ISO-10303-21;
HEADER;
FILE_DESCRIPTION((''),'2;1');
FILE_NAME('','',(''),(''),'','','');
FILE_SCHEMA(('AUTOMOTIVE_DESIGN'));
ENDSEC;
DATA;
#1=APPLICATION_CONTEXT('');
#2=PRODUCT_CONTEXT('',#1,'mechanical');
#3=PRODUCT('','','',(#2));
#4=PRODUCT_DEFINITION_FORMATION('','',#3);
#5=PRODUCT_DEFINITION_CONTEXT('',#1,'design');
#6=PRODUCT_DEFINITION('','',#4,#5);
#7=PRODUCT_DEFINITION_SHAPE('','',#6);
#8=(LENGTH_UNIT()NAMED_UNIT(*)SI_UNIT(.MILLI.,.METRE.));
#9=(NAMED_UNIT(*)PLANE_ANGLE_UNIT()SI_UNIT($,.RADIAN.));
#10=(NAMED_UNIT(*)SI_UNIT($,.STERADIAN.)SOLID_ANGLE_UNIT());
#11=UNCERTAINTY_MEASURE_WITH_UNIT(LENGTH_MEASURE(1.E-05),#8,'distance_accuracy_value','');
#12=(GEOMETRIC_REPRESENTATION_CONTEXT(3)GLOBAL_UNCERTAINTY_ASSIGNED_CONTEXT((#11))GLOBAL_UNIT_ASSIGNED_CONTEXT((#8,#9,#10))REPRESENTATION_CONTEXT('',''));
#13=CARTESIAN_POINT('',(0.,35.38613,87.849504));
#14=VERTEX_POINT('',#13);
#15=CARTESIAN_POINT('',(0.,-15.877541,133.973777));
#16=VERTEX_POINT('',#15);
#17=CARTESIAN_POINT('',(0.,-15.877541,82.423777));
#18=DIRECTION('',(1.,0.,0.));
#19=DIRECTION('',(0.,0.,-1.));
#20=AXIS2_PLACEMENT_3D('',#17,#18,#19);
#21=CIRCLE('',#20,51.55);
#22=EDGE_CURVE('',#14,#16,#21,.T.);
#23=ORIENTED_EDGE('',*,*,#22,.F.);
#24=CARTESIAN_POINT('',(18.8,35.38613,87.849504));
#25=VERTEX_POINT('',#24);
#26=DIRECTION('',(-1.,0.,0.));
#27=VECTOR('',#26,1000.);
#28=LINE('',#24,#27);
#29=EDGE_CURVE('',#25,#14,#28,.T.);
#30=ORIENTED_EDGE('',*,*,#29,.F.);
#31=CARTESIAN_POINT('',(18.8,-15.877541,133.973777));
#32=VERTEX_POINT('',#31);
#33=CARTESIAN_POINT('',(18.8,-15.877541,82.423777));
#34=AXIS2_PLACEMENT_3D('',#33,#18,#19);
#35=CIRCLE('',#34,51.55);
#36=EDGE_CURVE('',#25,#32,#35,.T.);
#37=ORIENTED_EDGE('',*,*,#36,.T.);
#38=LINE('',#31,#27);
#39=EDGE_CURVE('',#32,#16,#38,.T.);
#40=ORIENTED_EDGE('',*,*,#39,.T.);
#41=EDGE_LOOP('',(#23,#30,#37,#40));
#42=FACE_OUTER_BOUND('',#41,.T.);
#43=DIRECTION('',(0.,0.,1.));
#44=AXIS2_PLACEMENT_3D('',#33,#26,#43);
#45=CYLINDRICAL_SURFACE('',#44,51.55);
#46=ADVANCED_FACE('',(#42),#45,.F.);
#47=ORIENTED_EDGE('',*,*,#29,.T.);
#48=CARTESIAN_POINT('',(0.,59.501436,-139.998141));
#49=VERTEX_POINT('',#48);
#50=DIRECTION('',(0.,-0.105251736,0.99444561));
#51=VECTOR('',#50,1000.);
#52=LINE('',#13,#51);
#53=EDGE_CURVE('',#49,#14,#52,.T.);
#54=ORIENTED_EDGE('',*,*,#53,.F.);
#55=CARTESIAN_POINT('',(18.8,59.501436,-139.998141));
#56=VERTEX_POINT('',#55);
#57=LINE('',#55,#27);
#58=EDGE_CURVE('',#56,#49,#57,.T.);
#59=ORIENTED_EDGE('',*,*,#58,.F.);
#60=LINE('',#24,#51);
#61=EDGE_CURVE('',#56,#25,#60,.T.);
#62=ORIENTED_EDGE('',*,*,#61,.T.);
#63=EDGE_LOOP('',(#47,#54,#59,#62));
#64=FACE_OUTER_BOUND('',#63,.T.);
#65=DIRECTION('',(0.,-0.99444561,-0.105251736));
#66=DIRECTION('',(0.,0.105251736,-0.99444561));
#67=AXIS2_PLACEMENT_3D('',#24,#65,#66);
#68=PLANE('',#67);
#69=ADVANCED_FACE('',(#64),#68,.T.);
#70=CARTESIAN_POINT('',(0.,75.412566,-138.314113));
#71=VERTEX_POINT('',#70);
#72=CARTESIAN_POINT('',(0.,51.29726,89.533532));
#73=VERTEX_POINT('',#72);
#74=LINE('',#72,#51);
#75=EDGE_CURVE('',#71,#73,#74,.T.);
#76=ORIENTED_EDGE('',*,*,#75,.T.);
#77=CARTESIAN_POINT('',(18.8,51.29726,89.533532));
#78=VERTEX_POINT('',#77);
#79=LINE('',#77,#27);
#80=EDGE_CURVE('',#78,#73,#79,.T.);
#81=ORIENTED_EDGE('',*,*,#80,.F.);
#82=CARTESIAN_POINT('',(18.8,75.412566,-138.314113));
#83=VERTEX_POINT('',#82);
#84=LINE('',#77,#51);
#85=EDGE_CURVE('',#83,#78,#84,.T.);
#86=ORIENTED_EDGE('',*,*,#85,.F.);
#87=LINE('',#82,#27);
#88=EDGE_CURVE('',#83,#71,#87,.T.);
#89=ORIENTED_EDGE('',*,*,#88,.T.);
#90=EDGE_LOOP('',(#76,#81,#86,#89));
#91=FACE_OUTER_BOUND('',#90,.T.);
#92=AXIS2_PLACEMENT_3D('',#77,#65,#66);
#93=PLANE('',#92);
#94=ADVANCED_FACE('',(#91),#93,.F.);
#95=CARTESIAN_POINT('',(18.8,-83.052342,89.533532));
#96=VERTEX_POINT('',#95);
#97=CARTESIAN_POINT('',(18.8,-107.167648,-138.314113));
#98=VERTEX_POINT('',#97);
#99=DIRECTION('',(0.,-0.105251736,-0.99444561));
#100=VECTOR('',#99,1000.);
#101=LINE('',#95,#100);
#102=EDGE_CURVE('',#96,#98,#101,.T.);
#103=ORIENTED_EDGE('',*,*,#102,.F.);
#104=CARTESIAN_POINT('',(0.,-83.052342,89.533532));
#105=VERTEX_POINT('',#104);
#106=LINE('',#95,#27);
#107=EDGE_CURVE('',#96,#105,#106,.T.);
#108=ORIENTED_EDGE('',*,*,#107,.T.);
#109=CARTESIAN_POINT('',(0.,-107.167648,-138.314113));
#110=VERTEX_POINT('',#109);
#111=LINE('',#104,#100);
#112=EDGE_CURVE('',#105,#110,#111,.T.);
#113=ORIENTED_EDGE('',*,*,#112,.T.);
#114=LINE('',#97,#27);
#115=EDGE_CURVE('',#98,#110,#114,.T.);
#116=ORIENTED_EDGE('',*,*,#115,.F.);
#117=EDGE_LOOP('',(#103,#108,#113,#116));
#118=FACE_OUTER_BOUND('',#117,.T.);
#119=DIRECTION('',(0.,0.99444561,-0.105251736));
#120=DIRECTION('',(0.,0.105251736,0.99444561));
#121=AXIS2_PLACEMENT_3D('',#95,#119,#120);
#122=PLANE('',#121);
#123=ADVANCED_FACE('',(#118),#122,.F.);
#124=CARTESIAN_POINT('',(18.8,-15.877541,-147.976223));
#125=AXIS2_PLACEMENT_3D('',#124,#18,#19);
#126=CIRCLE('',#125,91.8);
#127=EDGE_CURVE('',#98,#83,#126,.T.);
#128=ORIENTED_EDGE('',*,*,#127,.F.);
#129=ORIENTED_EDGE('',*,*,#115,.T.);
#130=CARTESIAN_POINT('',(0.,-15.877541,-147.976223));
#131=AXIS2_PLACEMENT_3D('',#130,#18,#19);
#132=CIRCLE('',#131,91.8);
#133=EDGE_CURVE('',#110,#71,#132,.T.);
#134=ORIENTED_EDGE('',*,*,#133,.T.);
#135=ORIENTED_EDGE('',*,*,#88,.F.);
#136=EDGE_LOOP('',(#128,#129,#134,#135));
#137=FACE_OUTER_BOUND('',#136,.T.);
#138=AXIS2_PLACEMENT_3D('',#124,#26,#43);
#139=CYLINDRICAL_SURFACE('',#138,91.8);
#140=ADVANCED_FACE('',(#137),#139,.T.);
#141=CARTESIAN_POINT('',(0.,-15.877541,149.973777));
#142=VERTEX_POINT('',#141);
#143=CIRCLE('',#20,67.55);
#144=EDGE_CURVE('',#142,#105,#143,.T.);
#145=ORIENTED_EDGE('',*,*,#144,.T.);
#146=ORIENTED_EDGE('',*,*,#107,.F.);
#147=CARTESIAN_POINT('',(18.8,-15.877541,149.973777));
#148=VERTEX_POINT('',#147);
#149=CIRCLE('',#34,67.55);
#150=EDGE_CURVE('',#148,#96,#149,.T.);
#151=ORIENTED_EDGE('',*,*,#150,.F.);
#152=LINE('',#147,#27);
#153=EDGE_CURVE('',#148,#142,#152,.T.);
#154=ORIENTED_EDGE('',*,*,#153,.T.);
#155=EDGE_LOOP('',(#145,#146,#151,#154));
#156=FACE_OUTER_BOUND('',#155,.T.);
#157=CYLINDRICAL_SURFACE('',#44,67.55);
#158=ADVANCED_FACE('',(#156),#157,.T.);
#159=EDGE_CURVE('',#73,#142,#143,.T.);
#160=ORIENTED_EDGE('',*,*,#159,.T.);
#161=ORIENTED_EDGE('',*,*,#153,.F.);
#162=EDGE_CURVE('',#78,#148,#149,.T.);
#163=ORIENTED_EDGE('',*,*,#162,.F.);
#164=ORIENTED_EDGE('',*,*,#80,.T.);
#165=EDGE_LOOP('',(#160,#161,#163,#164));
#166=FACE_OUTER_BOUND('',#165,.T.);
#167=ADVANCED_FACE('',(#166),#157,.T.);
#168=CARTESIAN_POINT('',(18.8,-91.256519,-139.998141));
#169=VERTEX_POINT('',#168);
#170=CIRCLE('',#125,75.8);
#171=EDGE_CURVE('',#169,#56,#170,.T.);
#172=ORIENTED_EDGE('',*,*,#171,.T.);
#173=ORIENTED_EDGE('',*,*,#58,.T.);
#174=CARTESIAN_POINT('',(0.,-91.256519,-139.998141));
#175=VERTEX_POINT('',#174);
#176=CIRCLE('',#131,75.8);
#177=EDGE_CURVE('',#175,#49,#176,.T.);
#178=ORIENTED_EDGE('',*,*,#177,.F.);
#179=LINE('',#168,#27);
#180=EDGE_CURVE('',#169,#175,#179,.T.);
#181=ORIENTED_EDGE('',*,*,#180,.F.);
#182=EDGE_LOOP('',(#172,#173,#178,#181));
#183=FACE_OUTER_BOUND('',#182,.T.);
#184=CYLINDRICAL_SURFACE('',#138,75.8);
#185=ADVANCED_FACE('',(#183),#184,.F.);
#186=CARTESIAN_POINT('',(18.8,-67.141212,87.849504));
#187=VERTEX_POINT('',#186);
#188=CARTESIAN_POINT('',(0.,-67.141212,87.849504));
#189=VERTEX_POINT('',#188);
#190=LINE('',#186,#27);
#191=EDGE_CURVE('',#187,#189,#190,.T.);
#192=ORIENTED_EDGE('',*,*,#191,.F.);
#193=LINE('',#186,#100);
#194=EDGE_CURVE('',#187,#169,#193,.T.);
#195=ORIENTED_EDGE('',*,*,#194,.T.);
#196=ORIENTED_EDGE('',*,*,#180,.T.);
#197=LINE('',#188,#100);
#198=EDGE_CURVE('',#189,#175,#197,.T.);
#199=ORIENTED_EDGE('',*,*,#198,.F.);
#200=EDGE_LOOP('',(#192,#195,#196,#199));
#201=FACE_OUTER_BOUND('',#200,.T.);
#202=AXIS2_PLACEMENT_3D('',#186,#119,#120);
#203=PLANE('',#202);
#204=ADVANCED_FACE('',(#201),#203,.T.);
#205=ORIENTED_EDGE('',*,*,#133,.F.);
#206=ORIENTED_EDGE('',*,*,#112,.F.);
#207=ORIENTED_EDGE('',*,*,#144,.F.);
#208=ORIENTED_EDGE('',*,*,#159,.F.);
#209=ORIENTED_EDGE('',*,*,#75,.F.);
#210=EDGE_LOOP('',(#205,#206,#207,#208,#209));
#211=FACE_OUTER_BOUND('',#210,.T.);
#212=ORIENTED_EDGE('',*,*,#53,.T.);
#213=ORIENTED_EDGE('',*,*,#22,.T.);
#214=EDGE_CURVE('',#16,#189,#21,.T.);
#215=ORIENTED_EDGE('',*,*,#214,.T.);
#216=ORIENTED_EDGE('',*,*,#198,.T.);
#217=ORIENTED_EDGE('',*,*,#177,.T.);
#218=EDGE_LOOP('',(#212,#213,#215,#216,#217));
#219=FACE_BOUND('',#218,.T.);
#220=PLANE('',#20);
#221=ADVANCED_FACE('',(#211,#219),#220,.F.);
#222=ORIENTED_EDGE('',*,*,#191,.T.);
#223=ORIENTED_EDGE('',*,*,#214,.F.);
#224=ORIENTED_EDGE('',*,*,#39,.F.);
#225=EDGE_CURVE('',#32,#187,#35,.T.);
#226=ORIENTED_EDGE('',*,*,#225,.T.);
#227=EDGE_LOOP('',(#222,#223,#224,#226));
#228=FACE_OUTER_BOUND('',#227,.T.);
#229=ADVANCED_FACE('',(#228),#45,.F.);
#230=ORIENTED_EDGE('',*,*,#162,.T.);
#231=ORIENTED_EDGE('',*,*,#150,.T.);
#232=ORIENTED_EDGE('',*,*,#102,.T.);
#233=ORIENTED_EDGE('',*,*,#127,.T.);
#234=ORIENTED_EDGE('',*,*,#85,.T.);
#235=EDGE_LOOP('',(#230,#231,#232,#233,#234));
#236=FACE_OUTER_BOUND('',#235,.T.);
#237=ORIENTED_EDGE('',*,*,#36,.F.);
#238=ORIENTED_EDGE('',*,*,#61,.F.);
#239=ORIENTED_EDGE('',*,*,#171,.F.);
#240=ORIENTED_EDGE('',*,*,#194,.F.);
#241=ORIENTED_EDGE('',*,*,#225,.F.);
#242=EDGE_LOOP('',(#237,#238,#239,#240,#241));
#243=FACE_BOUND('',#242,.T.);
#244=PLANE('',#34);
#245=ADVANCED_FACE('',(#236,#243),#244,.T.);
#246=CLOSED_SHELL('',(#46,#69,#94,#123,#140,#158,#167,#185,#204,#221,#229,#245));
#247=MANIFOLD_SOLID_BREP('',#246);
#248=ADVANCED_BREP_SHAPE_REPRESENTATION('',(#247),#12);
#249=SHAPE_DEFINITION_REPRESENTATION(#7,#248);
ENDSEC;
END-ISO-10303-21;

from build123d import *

# Parameters (mm, degrees)
EXTRUDE_1_DEPTH = 18.8


with BuildPart() as part:
    # 草图1 → 拉伸-薄壁1 (new body)
    with BuildSketch(Plane(origin=(0, 0, 0), x_dir=(0, 0, -1), z_dir=(1, 0, 0))):
        with BuildLine():
            Line((138.314113207, -107.167648268), (-89.533532193, -83.052342215))
            ThreePointArc((-89.533532193, -83.052342215), (-149.973777418, -15.877541233), (-89.533532193, 51.29725975))
            Line((-89.533532193, 51.29725975), (138.314113207, 75.412565802))
            ThreePointArc((138.314113207, 75.412565802), (239.776222582, -15.877541233), (138.314113207, -107.167648268))
        make_face()
        with BuildLine():
            Line((139.998140985, -91.256518501), (-87.849504415, -67.141212449))
            ThreePointArc((-87.849504415, -67.141212449), (-133.973777418, -15.877541233), (-87.849504415, 35.386129983))
            Line((-87.849504415, 35.386129983), (139.998140985, 59.501436035))
            ThreePointArc((139.998140985, 59.501436035), (223.776222582, -15.877541233), (139.998140985, -91.256518501))
        make_face(mode=Mode.SUBTRACT)
    extrude(amount=EXTRUDE_1_DEPTH)


solid = part.part
